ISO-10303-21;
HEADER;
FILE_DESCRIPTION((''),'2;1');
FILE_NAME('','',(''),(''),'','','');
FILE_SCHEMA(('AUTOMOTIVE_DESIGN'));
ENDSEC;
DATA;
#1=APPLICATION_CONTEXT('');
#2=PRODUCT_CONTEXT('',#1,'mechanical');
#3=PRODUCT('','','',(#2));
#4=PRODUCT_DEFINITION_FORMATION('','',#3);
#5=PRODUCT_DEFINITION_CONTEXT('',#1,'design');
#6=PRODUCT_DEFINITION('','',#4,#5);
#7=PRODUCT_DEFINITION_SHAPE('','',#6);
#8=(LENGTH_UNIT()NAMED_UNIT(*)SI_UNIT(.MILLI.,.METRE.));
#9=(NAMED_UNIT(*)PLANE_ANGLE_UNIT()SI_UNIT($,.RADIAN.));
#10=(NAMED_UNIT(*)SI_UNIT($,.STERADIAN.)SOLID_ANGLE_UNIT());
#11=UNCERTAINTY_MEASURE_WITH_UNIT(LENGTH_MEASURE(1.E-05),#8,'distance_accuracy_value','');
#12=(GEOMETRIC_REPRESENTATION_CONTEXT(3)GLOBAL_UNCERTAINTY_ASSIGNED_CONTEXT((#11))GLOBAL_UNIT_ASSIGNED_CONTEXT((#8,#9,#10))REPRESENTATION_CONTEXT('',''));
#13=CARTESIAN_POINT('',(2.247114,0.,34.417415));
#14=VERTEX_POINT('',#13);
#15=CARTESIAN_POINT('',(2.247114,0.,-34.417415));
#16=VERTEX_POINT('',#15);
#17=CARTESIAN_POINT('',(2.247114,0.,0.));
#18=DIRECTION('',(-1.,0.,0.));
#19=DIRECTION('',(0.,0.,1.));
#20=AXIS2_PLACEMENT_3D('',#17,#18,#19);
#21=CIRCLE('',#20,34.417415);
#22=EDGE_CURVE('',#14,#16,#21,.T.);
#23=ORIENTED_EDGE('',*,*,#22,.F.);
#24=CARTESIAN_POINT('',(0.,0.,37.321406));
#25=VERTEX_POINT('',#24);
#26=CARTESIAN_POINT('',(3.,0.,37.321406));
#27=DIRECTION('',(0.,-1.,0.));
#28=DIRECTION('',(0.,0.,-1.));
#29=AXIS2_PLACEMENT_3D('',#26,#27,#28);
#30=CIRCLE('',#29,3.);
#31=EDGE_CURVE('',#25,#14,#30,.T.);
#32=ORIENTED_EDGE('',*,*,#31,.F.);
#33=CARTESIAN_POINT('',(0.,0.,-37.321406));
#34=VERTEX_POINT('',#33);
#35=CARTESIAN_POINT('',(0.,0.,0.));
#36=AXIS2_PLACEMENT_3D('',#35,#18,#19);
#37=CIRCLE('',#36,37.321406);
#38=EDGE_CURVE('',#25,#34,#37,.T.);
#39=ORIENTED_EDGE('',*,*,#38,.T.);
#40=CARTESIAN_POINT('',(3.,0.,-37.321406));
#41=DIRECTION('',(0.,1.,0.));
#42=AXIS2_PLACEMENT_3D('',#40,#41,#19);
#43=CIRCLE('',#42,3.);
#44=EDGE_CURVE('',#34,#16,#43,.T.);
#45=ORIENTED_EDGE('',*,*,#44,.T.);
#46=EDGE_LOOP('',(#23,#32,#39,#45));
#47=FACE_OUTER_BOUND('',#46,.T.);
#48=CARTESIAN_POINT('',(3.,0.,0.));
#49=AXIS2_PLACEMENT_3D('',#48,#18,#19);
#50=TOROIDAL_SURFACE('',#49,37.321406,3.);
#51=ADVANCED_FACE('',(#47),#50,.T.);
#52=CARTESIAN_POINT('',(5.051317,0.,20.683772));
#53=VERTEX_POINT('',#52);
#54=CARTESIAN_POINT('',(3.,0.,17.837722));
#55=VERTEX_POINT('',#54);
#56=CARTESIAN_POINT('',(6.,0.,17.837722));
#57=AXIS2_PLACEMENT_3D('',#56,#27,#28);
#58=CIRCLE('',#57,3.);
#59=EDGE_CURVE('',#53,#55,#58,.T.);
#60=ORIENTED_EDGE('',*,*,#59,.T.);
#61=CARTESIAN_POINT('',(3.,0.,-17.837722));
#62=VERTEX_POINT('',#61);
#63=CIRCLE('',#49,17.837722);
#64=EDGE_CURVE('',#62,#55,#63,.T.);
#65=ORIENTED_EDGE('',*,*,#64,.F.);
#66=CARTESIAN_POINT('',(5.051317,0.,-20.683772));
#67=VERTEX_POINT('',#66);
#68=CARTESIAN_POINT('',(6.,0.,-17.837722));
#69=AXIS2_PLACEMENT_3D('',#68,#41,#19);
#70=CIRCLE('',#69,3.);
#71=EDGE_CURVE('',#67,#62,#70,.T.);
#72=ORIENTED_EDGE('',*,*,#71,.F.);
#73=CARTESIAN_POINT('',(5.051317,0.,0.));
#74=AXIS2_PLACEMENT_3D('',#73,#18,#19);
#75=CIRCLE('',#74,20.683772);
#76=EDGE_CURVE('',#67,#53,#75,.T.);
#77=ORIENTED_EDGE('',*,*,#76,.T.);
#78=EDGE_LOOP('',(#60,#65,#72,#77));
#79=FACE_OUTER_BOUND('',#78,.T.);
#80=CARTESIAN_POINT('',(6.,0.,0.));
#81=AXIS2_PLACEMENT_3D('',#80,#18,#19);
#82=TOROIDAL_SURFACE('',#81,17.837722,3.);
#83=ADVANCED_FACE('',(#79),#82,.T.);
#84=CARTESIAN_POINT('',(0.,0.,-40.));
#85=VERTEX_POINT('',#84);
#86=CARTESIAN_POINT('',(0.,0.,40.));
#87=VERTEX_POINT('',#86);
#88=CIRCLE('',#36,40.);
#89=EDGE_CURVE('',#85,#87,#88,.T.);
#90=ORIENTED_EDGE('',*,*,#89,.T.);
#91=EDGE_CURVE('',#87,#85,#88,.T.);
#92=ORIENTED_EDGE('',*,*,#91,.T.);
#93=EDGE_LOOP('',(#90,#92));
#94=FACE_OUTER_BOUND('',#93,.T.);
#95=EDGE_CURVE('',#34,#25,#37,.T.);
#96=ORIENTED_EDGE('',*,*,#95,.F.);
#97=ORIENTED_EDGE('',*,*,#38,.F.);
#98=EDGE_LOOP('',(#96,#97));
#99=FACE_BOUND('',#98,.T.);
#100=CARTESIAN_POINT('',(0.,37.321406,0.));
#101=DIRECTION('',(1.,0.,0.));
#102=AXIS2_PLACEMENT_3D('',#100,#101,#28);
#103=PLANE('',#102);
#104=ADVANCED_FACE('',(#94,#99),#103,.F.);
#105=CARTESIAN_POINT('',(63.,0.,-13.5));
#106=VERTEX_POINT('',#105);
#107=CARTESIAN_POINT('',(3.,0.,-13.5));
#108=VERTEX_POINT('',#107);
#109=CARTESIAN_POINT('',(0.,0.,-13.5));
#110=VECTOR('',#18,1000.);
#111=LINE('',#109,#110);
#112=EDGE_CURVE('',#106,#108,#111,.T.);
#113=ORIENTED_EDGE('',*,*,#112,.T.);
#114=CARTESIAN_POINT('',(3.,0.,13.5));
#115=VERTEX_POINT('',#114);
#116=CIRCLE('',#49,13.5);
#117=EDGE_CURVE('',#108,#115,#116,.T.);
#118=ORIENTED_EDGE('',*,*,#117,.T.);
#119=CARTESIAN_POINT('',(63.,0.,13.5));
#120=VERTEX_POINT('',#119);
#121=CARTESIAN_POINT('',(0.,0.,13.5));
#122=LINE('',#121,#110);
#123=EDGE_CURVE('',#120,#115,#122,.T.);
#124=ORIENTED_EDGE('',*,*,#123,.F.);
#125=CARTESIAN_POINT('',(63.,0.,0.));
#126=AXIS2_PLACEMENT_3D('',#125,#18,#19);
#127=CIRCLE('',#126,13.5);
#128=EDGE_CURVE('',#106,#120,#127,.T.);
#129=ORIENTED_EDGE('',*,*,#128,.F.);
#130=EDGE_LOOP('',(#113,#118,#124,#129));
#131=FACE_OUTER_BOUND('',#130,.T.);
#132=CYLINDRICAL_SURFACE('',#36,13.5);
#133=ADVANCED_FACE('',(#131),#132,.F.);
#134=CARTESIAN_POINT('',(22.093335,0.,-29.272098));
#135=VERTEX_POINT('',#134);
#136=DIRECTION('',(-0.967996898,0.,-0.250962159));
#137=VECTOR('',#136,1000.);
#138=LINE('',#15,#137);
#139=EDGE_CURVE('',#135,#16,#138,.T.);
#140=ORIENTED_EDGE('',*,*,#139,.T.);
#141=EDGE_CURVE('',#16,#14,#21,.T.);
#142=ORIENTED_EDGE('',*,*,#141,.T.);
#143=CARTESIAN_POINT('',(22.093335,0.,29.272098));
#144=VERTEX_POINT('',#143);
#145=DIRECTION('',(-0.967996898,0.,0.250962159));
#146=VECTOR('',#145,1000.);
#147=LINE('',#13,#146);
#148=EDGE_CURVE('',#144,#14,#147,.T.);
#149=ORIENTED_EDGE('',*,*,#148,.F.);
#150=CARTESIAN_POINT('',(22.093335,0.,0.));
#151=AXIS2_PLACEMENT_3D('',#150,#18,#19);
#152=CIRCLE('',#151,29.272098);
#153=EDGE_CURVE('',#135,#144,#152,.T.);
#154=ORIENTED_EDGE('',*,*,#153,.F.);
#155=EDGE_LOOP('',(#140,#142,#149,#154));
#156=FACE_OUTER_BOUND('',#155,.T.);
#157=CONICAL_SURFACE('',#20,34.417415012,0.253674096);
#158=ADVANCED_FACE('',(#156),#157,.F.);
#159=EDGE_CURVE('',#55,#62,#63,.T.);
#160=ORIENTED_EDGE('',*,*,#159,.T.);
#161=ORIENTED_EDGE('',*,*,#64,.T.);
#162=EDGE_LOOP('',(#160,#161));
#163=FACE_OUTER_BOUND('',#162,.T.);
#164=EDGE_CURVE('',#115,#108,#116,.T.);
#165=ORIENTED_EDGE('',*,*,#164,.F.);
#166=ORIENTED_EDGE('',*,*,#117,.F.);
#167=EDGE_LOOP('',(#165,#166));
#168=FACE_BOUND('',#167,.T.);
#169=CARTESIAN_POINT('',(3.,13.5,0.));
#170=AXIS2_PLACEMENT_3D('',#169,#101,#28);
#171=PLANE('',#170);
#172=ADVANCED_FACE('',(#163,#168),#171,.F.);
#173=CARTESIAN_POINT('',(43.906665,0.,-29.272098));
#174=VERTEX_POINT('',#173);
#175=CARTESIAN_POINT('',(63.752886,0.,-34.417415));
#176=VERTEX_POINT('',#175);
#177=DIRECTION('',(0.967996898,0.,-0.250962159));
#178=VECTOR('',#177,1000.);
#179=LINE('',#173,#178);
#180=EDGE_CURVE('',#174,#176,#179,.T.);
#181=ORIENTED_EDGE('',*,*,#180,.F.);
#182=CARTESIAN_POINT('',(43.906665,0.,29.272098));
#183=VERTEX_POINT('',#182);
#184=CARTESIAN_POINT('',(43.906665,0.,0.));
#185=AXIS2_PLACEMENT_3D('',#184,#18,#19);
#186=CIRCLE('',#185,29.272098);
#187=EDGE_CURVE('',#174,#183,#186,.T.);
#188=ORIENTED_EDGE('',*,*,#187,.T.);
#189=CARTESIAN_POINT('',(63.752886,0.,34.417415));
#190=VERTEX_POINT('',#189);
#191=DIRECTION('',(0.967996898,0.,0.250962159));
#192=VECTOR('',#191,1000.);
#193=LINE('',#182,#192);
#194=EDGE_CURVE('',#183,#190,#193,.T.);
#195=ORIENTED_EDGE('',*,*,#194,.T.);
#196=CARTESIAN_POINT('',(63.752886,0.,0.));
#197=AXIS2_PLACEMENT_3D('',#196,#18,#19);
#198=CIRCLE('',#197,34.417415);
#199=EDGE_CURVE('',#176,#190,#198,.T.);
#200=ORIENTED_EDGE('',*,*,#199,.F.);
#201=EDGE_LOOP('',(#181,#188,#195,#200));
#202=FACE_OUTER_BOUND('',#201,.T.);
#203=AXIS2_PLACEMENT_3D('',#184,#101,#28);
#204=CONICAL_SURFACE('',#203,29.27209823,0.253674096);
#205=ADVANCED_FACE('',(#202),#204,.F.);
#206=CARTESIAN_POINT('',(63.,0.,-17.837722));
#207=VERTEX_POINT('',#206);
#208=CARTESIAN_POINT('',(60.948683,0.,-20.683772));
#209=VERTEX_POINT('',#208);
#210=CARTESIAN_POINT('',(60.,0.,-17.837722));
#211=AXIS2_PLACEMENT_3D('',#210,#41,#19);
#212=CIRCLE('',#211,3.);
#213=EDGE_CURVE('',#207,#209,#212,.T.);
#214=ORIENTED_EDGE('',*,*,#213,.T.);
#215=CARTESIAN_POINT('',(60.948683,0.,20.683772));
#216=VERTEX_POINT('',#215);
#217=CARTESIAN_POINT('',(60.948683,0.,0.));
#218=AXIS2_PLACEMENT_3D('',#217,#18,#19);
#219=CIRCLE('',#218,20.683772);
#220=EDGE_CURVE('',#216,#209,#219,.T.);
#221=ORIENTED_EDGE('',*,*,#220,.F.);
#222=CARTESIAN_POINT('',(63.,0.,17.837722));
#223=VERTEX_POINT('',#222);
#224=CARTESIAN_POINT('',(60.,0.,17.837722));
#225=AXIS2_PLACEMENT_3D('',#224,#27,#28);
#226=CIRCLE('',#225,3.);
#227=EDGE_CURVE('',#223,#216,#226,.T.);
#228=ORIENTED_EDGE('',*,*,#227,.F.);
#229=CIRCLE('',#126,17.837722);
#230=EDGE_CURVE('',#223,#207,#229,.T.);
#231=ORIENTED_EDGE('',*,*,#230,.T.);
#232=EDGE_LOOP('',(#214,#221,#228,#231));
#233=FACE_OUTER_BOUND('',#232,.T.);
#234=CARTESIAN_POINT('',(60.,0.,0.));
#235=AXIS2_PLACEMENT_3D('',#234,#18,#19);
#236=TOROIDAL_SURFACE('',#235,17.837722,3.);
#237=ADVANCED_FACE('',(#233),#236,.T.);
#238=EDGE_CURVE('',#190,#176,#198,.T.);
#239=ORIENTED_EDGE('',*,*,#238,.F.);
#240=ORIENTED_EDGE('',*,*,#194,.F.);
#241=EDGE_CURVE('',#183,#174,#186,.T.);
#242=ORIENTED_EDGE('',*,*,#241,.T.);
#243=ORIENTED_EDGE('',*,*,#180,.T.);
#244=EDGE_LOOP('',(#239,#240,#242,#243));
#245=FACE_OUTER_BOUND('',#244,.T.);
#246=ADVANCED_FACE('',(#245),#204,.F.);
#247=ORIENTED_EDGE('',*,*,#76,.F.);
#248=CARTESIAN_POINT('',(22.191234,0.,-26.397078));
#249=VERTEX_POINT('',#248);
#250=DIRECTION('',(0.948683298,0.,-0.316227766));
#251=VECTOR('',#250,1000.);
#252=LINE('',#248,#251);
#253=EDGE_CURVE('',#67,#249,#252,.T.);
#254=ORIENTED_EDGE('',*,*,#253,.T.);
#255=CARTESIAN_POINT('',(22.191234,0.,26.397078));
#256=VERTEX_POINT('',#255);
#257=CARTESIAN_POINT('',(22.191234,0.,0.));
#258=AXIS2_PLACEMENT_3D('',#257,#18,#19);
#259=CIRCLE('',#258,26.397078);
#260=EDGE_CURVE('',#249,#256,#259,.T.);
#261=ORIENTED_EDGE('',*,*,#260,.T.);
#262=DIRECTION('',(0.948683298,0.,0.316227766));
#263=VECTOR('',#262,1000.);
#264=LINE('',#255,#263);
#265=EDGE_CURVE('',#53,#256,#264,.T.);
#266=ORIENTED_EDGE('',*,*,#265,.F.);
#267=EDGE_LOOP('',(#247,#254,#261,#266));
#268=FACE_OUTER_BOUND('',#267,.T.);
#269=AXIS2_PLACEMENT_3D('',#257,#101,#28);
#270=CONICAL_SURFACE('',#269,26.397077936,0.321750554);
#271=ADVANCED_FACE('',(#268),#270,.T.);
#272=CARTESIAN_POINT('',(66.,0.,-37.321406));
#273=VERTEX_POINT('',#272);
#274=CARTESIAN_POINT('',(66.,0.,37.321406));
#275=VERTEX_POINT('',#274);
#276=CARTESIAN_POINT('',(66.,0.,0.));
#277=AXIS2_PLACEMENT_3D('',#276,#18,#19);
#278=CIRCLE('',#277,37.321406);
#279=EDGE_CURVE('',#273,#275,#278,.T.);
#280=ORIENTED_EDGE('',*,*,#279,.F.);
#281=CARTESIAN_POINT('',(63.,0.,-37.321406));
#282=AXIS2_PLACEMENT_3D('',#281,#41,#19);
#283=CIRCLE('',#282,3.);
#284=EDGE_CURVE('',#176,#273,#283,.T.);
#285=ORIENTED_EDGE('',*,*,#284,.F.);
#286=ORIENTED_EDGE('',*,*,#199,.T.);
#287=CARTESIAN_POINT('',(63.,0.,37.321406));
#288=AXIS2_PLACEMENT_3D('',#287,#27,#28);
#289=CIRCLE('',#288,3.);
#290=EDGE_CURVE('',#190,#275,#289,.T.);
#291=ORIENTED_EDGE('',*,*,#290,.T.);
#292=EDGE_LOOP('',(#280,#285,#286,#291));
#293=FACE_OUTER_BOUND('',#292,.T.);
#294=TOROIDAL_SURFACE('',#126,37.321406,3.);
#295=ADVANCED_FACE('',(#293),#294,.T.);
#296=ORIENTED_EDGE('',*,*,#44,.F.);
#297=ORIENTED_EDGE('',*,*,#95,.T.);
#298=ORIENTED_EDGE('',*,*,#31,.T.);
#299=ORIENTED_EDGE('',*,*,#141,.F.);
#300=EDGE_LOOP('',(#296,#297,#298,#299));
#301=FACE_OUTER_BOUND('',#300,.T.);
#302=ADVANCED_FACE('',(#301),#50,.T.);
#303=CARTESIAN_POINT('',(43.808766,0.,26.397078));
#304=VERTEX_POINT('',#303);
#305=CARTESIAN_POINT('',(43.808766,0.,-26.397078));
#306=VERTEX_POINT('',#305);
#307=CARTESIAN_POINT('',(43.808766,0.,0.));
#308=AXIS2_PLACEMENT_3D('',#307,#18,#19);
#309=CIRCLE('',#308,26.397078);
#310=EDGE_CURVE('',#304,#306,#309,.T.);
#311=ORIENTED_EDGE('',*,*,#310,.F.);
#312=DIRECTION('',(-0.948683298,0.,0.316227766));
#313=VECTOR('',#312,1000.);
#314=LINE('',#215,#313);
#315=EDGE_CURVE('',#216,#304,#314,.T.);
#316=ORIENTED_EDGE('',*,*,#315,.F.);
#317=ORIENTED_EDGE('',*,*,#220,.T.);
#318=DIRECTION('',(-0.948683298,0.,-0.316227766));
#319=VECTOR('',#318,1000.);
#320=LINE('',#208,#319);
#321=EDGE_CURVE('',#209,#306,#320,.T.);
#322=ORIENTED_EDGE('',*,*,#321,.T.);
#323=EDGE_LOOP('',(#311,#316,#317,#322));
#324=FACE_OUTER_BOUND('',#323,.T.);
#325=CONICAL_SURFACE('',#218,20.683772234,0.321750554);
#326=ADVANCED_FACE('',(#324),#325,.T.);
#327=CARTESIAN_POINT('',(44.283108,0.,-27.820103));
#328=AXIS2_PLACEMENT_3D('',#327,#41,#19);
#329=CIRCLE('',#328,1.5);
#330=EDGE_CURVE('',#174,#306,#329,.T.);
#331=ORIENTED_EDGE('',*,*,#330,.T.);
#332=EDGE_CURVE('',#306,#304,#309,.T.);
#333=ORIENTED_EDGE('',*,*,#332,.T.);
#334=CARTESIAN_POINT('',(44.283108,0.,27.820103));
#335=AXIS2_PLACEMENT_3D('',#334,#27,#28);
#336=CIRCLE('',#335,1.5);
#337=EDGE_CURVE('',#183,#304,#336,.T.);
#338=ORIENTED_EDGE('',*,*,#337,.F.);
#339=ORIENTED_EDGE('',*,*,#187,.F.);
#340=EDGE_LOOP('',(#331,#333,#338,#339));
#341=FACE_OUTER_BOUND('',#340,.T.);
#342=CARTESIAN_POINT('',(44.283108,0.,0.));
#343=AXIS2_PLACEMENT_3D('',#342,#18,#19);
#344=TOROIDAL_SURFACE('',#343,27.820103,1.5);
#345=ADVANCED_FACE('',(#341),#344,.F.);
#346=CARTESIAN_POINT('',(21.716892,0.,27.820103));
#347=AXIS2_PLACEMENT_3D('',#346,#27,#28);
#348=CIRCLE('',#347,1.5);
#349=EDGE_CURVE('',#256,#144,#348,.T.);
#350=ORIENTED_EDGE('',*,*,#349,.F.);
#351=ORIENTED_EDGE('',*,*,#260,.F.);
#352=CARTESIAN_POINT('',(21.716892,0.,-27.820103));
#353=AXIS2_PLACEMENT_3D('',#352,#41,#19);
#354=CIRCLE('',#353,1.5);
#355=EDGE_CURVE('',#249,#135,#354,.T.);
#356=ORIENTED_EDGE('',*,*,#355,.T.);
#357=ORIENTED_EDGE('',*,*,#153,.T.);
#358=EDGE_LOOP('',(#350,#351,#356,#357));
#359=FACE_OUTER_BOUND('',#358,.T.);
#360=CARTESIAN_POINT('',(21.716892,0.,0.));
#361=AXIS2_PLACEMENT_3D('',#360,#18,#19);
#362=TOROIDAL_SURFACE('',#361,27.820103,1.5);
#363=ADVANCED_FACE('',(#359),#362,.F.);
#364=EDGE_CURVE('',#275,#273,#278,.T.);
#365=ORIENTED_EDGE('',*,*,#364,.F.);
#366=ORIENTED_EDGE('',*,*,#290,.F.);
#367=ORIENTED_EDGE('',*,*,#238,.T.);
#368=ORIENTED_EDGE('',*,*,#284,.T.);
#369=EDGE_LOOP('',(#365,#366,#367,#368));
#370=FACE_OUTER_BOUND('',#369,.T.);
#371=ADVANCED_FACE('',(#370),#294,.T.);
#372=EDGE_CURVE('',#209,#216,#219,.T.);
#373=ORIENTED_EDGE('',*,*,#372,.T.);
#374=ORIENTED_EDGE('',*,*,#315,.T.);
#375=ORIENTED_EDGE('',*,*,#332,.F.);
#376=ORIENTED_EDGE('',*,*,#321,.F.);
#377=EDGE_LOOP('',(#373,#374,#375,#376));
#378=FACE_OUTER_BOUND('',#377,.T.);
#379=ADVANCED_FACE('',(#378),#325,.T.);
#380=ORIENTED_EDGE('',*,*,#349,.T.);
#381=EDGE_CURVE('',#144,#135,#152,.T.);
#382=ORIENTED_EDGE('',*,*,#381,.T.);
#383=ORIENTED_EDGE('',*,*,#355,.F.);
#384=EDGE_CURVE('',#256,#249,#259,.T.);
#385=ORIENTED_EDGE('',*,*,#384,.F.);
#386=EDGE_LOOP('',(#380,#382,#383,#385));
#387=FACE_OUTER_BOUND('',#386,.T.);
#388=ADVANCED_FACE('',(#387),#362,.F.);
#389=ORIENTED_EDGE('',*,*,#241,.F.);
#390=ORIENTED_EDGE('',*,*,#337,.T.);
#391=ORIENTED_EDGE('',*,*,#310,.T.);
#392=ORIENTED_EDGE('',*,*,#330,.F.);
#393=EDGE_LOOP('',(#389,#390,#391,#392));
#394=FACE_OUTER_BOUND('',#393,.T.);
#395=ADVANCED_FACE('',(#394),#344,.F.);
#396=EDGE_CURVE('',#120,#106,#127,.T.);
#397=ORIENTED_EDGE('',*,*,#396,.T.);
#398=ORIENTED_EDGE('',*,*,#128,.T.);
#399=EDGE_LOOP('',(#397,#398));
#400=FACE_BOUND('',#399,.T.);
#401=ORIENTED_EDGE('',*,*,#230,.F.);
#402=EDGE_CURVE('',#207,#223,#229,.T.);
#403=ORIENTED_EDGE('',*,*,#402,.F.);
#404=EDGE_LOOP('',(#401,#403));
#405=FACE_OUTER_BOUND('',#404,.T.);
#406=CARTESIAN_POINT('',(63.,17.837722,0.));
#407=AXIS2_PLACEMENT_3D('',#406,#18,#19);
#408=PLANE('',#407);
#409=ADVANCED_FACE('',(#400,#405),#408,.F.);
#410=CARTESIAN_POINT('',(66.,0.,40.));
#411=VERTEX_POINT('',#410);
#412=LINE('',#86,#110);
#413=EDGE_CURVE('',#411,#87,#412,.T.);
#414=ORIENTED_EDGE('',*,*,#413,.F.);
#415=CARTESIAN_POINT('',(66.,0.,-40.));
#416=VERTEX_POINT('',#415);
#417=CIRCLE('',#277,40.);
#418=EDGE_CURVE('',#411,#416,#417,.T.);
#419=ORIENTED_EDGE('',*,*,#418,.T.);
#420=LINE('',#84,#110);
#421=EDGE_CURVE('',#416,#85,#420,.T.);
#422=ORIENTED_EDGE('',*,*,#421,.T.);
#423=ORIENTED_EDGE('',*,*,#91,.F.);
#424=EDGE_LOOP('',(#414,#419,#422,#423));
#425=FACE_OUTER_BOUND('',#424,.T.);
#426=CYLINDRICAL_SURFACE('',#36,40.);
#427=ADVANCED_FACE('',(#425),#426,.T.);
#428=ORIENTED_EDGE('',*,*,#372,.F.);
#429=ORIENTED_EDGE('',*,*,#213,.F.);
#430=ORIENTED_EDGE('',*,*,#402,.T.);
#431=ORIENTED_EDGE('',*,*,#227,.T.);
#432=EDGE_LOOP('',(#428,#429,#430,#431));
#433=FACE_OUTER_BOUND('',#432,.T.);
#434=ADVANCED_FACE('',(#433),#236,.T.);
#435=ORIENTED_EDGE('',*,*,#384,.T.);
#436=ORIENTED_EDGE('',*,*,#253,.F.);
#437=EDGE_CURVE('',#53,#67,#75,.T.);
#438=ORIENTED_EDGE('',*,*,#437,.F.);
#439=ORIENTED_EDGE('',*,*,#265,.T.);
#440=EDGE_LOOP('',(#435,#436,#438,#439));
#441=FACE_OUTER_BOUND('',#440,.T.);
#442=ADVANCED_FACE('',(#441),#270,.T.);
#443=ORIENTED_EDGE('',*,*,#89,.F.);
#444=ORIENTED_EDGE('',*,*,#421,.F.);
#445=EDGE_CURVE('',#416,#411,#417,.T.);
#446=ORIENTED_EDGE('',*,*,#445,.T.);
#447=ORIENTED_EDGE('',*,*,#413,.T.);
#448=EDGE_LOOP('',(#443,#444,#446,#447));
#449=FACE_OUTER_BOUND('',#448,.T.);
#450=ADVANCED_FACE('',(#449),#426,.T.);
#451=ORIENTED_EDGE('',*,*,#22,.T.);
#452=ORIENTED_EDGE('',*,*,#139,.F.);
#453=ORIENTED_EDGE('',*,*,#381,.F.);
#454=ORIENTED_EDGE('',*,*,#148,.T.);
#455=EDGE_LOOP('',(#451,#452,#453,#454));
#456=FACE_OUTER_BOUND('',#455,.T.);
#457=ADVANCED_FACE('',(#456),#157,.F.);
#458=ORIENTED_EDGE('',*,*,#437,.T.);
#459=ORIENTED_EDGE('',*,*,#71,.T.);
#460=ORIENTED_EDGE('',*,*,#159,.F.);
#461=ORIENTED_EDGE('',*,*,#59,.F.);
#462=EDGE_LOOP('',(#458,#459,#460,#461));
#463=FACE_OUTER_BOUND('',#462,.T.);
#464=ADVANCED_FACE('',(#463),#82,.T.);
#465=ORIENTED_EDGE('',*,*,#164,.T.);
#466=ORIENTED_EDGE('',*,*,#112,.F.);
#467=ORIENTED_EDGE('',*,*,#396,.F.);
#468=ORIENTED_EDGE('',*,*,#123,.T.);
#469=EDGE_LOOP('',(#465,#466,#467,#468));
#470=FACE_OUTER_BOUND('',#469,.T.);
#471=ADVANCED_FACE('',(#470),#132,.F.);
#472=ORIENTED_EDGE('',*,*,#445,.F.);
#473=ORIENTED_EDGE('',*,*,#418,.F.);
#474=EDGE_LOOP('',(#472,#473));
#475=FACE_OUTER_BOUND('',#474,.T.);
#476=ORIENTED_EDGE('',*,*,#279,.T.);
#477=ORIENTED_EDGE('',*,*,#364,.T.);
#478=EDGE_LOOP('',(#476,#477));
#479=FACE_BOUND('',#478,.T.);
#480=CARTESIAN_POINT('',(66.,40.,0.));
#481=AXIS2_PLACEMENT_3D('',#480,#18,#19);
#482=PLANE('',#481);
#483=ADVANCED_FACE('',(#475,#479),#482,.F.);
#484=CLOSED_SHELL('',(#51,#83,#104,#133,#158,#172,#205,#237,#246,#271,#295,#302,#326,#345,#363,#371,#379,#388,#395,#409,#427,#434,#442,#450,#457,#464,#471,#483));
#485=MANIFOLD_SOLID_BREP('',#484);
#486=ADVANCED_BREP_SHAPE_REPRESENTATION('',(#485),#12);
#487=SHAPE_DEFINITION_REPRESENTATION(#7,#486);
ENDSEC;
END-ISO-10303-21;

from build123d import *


with BuildPart() as part:
    # Sketch1 → Revolve1 (revolve)
    with BuildSketch(Plane.XY, mode=Mode.PRIVATE) as revolve1_sk:
        with BuildLine():
            Line((0, 40), (66, 40))
            Line((66, 40), (66, 37.321405707))
            ThreePointArc((66, 37.321405707), (65.372620854, 35.485467177), (63.752886476, 34.417415012))
            Line((63.752886476, 34.417415012), (43.906664603, 29.27209823))
            ThreePointArc((43.906664603, 29.27209823), (42.783976708, 27.871150368), (43.808766192, 26.397077936))
            Line((43.808766192, 26.397077936), (60.948683298, 20.683772234))
            ThreePointArc((60.948683298, 20.683772234), (62.433726556, 19.591853194), (63, 17.83772234))
            Line((63, 17.83772234), (63, 13.5))
            Line((63, 13.5), (3, 13.5))
            Line((3, 13.5), (3, 17.83772234))
            ThreePointArc((3, 17.83772234), (3.566273444, 19.591853194), (5.051316702, 20.683772234))
            Line((5.051316702, 20.683772234), (22.191233808, 26.397077936))
            ThreePointArc((22.191233808, 26.397077936), (23.216023292, 27.871150368), (22.093335397, 29.27209823))
            Line((22.093335397, 29.27209823), (2.247113524, 34.417415012))
            ThreePointArc((2.247113524, 34.417415012), (0.627379146, 35.485467177), (0, 37.321405707))
            Line((0, 37.321405707), (0, 40))
        make_face()
    revolve(revolve1_sk.sketch.rotate(Axis((0, 0, 0), (1, 0, 0)), 90), axis=Axis((0, 0, 0), (1, 0, 0)))


solid = part.part
